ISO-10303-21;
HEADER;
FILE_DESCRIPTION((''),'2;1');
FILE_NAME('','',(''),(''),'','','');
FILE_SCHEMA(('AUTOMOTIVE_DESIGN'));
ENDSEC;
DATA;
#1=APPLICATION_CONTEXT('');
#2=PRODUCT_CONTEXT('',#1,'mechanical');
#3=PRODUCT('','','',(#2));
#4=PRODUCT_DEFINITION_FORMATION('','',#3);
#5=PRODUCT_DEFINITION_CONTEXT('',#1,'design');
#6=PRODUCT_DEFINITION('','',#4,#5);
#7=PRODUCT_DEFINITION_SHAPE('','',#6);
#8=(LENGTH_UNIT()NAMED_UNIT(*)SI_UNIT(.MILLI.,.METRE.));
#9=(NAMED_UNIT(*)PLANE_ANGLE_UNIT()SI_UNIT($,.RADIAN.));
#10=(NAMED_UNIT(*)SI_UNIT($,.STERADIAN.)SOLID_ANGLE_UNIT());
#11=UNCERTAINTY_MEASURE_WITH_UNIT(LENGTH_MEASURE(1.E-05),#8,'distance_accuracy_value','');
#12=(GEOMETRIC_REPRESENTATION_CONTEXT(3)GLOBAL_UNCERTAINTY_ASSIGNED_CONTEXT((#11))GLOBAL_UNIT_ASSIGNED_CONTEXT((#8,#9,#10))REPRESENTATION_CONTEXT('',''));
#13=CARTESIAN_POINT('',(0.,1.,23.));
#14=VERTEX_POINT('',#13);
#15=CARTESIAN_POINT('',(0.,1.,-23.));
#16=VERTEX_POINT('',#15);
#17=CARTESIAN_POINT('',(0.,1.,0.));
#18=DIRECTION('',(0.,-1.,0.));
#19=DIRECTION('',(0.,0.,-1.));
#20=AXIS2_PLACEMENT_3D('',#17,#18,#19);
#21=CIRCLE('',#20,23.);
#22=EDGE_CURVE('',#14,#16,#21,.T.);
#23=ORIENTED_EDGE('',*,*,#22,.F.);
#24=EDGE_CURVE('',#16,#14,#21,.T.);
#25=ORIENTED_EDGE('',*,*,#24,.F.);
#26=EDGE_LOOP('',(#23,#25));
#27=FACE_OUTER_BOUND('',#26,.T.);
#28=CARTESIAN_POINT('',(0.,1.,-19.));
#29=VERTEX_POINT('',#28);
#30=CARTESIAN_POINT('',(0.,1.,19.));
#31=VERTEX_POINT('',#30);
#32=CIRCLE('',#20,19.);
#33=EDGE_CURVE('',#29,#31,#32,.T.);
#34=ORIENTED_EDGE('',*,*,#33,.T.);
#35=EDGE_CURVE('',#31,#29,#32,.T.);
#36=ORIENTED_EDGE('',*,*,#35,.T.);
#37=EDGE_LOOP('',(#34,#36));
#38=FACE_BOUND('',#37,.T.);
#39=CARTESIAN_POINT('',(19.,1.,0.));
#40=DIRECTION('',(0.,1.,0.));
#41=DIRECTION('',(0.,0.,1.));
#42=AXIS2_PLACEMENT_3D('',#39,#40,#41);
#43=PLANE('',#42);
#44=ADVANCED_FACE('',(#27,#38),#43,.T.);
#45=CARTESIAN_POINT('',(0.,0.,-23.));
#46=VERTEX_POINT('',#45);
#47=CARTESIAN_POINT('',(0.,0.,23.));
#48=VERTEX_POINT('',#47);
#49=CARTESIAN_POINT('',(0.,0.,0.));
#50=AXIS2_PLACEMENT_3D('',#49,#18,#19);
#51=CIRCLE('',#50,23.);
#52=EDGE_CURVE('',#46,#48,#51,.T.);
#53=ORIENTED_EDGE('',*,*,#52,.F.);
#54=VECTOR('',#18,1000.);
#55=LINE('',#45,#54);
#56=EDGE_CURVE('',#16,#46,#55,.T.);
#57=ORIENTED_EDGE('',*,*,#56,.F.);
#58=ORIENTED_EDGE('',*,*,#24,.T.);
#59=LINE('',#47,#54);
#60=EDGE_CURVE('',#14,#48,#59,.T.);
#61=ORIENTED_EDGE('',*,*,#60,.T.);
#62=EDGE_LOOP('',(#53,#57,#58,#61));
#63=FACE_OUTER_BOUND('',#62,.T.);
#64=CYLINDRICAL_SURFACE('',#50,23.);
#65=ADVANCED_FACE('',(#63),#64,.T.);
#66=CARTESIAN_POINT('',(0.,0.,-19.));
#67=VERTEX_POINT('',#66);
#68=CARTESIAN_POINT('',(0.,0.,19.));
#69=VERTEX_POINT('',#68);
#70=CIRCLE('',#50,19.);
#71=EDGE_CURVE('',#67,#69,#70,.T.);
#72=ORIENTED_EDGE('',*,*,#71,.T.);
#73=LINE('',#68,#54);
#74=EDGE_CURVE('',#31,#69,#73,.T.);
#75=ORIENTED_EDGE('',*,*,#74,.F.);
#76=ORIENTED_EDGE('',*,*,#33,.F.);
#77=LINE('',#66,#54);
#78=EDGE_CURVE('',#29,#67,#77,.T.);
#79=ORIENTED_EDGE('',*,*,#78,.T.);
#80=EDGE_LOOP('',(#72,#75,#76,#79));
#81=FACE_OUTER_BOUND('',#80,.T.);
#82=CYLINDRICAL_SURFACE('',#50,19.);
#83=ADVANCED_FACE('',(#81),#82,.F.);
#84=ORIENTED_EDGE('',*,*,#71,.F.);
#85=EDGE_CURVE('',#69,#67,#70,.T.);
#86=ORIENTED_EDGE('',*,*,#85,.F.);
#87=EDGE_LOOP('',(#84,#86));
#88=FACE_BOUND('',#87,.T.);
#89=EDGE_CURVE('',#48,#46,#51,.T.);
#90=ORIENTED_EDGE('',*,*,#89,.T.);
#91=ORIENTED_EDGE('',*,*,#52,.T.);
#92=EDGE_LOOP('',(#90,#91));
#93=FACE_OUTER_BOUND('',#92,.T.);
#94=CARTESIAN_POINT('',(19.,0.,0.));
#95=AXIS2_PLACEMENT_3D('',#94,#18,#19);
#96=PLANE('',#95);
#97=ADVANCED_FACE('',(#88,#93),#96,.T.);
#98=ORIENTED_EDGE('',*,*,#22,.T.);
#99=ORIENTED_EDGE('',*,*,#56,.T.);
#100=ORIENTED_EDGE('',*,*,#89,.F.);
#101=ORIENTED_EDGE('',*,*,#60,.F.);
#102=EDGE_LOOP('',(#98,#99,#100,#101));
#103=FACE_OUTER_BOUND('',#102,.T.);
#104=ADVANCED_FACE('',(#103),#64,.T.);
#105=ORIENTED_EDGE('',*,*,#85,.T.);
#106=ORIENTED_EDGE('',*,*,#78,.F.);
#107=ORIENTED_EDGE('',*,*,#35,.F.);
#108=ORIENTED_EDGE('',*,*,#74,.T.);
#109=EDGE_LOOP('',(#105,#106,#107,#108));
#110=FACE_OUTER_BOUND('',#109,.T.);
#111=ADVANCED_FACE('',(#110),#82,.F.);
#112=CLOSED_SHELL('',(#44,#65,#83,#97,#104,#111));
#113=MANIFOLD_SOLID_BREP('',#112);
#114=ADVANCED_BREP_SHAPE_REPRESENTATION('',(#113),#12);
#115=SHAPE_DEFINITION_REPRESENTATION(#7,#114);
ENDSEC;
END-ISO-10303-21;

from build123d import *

# Parameters (mm, degrees)
SKETCH1_W = 4
SKETCH1_H = 1


with BuildPart() as part:
    # Sketch1 → Revolve1 (revolve)
    with BuildSketch(Plane.XY, mode=Mode.PRIVATE) as revolve1_sk:
        with Locations((21, 0.5)):
            Rectangle(SKETCH1_W, SKETCH1_H)
    revolve(revolve1_sk.sketch.rotate(Axis((0, 0, 0), (0, 1, 0)), 90), axis=Axis((0, 0, 0), (0, 1, 0)))


solid = part.part
